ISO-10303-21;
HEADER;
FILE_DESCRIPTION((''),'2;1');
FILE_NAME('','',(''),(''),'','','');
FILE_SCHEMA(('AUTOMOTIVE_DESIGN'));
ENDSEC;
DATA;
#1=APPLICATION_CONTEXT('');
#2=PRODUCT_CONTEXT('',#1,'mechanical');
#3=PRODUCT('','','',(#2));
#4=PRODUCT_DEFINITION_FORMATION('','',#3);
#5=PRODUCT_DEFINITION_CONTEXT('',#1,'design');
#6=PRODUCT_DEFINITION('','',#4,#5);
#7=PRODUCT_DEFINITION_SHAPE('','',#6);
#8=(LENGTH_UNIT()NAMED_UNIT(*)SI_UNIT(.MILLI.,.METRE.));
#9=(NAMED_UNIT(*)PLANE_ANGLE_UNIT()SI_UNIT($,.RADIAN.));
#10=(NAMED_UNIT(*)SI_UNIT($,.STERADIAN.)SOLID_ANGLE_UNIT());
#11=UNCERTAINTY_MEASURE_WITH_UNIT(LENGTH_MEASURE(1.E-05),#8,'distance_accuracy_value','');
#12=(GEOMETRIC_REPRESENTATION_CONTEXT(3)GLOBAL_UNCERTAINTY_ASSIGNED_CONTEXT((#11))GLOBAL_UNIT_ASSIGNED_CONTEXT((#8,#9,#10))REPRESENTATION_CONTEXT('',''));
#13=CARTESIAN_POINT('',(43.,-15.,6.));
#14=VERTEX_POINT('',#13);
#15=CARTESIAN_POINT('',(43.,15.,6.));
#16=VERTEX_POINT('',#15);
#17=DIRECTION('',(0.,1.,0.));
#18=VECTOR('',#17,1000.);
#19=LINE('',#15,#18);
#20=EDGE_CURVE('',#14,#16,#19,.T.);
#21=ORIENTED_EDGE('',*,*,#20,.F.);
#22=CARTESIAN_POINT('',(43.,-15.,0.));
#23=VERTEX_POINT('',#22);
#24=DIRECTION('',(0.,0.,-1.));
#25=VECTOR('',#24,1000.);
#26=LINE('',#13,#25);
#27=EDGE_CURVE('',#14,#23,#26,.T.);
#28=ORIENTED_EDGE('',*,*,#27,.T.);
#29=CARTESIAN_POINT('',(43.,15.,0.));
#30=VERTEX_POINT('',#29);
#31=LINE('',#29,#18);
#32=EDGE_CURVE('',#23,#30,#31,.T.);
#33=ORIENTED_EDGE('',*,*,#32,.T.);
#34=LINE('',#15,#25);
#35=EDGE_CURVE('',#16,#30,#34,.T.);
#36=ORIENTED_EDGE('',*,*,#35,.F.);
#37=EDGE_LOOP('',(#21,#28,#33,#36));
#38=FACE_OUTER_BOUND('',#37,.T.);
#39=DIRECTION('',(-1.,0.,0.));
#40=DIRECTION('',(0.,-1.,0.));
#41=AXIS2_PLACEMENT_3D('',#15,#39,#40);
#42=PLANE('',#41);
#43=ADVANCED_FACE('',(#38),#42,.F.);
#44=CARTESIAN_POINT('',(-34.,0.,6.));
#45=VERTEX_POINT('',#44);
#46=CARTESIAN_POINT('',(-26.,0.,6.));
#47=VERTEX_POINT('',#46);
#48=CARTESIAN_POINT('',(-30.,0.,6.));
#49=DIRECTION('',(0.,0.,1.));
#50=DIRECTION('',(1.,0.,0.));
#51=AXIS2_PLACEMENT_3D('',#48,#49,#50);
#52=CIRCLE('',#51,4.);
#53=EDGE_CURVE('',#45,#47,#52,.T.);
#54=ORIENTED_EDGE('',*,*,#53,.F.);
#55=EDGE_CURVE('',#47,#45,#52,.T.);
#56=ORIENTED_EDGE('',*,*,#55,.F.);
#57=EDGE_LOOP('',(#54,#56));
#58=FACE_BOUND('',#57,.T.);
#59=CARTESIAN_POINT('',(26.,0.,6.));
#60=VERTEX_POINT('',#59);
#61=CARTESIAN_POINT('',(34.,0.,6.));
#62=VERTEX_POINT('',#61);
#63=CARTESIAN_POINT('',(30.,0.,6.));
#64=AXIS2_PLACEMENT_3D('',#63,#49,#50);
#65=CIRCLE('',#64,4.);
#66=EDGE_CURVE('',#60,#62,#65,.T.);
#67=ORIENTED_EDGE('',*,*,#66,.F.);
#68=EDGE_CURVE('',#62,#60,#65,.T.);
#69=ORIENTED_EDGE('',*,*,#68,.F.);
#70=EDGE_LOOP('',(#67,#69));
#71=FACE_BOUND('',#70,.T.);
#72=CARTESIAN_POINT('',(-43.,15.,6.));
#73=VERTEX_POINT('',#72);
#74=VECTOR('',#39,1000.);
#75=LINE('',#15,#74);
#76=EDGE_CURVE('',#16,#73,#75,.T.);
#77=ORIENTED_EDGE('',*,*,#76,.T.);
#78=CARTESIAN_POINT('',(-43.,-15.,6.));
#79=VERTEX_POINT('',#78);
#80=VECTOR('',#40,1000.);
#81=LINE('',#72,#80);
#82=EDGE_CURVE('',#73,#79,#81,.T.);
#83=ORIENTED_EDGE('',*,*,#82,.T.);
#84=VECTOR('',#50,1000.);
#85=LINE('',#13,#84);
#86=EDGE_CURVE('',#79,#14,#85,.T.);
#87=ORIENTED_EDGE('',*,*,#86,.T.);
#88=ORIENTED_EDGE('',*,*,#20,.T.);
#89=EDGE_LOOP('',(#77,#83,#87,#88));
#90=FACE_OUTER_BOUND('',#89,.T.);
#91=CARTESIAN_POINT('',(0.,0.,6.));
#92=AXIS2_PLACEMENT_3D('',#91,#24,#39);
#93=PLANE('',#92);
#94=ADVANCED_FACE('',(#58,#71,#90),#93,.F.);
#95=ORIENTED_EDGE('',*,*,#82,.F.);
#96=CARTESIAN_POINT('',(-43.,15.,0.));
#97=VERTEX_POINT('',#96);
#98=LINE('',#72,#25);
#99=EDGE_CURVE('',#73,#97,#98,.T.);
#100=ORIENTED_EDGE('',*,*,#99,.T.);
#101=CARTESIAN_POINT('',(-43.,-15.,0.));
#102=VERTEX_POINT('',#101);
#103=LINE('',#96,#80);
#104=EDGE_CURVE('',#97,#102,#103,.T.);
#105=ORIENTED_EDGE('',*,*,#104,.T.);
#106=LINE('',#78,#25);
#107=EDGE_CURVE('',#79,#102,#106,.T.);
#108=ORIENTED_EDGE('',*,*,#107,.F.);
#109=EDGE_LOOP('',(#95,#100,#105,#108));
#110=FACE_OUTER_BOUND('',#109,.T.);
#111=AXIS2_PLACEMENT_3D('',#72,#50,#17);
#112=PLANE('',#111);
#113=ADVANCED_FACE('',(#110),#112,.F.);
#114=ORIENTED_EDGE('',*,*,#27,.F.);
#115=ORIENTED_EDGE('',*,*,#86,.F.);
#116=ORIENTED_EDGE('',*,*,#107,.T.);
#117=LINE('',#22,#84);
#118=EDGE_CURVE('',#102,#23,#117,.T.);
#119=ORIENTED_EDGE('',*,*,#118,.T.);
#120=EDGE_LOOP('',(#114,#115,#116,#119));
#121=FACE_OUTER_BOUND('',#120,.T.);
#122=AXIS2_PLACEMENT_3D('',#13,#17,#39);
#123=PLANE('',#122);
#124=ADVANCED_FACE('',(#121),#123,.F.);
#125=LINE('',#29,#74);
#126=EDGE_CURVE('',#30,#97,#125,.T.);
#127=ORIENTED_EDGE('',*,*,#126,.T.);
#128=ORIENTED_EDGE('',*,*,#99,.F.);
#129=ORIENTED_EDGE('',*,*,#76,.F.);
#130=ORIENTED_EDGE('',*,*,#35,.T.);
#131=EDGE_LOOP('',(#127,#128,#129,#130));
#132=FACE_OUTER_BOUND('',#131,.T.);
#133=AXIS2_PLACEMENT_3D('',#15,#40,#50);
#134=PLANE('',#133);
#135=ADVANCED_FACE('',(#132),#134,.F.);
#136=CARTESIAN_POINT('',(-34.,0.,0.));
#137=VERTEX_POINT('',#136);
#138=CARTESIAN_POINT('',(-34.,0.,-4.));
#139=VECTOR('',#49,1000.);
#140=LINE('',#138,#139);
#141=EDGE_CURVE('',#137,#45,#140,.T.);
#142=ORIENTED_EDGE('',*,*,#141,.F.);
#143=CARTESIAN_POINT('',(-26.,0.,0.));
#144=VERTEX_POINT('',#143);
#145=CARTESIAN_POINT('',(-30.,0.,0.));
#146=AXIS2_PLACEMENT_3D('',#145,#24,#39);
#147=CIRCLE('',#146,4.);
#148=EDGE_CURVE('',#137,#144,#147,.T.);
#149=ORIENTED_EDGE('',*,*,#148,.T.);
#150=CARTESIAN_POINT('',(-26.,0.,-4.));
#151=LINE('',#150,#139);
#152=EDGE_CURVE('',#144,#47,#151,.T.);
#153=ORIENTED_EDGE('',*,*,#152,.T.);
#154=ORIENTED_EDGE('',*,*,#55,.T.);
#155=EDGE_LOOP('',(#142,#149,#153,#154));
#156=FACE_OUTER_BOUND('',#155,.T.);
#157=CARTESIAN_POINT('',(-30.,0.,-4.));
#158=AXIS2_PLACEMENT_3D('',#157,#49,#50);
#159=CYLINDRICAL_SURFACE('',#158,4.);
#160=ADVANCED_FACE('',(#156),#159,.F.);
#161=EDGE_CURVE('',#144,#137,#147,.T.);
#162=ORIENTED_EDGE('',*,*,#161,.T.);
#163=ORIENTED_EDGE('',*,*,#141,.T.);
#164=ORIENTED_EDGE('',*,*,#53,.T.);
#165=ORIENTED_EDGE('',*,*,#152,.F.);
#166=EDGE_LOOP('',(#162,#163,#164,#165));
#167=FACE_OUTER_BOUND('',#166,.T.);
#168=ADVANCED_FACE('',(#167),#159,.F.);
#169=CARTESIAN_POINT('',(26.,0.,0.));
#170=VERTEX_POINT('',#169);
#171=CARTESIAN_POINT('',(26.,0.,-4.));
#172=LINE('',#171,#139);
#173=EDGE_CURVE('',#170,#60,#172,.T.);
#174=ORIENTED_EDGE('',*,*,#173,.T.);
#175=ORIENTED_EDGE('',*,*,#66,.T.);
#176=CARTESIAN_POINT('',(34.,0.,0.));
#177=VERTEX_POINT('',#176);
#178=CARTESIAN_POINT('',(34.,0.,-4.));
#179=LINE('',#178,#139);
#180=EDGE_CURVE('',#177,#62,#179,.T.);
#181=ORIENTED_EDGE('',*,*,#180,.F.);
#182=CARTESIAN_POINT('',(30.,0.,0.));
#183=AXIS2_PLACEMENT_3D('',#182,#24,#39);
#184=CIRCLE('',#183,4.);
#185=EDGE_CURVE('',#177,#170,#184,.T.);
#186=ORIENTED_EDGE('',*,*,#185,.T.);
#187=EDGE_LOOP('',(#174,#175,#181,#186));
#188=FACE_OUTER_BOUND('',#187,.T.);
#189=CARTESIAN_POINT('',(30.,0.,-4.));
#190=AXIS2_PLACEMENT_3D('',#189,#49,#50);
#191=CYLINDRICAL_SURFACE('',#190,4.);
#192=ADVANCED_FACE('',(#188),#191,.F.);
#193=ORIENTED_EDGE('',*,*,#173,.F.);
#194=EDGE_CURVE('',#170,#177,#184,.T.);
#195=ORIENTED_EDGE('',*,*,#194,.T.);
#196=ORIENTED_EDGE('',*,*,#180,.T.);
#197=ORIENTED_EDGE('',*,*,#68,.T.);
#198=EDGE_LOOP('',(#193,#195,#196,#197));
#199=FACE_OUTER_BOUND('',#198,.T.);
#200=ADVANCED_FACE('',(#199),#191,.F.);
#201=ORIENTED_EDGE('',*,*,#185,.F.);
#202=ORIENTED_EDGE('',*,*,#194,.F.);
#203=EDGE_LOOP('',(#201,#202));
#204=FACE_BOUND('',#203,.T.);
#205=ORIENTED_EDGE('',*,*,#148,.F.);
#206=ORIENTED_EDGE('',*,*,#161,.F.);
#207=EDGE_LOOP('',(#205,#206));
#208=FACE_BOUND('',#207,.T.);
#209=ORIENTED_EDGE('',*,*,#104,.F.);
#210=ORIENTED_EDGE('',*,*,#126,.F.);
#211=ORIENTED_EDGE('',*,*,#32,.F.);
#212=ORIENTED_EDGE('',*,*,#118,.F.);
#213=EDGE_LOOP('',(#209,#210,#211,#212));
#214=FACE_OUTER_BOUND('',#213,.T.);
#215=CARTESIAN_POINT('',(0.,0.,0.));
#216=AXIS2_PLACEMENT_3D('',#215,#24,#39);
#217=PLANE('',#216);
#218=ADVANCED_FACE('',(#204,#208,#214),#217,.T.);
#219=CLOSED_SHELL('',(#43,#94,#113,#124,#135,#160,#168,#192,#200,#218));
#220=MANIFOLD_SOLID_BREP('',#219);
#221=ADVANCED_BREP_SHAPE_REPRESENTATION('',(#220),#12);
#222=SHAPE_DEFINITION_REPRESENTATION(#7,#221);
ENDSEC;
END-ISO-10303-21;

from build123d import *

# Parameters (mm, degrees)
SKETCH1_W           = 86
SKETCH1_H           = 30
BOSS_EXTRUDE1_DEPTH = 6
SKETCH2_R           = 4
CUT_EXTRUDE1_DEPTH  = 10


with BuildPart() as part:
    # Sketch1 → Boss-Extrude1 (new body)
    with BuildSketch(Plane.XY):
        Rectangle(SKETCH1_W, SKETCH1_H)
    extrude(amount=BOSS_EXTRUDE1_DEPTH)

    # Sketch2 → Cut-Extrude1 (cut)
    with BuildSketch(Plane.XY.offset(6)):
        with Locations((-30, 0)):
            Circle(SKETCH2_R)
        with Locations((30, 0)):
            Circle(SKETCH2_R)
    extrude(amount=-CUT_EXTRUDE1_DEPTH, mode=Mode.SUBTRACT)


solid = part.part
